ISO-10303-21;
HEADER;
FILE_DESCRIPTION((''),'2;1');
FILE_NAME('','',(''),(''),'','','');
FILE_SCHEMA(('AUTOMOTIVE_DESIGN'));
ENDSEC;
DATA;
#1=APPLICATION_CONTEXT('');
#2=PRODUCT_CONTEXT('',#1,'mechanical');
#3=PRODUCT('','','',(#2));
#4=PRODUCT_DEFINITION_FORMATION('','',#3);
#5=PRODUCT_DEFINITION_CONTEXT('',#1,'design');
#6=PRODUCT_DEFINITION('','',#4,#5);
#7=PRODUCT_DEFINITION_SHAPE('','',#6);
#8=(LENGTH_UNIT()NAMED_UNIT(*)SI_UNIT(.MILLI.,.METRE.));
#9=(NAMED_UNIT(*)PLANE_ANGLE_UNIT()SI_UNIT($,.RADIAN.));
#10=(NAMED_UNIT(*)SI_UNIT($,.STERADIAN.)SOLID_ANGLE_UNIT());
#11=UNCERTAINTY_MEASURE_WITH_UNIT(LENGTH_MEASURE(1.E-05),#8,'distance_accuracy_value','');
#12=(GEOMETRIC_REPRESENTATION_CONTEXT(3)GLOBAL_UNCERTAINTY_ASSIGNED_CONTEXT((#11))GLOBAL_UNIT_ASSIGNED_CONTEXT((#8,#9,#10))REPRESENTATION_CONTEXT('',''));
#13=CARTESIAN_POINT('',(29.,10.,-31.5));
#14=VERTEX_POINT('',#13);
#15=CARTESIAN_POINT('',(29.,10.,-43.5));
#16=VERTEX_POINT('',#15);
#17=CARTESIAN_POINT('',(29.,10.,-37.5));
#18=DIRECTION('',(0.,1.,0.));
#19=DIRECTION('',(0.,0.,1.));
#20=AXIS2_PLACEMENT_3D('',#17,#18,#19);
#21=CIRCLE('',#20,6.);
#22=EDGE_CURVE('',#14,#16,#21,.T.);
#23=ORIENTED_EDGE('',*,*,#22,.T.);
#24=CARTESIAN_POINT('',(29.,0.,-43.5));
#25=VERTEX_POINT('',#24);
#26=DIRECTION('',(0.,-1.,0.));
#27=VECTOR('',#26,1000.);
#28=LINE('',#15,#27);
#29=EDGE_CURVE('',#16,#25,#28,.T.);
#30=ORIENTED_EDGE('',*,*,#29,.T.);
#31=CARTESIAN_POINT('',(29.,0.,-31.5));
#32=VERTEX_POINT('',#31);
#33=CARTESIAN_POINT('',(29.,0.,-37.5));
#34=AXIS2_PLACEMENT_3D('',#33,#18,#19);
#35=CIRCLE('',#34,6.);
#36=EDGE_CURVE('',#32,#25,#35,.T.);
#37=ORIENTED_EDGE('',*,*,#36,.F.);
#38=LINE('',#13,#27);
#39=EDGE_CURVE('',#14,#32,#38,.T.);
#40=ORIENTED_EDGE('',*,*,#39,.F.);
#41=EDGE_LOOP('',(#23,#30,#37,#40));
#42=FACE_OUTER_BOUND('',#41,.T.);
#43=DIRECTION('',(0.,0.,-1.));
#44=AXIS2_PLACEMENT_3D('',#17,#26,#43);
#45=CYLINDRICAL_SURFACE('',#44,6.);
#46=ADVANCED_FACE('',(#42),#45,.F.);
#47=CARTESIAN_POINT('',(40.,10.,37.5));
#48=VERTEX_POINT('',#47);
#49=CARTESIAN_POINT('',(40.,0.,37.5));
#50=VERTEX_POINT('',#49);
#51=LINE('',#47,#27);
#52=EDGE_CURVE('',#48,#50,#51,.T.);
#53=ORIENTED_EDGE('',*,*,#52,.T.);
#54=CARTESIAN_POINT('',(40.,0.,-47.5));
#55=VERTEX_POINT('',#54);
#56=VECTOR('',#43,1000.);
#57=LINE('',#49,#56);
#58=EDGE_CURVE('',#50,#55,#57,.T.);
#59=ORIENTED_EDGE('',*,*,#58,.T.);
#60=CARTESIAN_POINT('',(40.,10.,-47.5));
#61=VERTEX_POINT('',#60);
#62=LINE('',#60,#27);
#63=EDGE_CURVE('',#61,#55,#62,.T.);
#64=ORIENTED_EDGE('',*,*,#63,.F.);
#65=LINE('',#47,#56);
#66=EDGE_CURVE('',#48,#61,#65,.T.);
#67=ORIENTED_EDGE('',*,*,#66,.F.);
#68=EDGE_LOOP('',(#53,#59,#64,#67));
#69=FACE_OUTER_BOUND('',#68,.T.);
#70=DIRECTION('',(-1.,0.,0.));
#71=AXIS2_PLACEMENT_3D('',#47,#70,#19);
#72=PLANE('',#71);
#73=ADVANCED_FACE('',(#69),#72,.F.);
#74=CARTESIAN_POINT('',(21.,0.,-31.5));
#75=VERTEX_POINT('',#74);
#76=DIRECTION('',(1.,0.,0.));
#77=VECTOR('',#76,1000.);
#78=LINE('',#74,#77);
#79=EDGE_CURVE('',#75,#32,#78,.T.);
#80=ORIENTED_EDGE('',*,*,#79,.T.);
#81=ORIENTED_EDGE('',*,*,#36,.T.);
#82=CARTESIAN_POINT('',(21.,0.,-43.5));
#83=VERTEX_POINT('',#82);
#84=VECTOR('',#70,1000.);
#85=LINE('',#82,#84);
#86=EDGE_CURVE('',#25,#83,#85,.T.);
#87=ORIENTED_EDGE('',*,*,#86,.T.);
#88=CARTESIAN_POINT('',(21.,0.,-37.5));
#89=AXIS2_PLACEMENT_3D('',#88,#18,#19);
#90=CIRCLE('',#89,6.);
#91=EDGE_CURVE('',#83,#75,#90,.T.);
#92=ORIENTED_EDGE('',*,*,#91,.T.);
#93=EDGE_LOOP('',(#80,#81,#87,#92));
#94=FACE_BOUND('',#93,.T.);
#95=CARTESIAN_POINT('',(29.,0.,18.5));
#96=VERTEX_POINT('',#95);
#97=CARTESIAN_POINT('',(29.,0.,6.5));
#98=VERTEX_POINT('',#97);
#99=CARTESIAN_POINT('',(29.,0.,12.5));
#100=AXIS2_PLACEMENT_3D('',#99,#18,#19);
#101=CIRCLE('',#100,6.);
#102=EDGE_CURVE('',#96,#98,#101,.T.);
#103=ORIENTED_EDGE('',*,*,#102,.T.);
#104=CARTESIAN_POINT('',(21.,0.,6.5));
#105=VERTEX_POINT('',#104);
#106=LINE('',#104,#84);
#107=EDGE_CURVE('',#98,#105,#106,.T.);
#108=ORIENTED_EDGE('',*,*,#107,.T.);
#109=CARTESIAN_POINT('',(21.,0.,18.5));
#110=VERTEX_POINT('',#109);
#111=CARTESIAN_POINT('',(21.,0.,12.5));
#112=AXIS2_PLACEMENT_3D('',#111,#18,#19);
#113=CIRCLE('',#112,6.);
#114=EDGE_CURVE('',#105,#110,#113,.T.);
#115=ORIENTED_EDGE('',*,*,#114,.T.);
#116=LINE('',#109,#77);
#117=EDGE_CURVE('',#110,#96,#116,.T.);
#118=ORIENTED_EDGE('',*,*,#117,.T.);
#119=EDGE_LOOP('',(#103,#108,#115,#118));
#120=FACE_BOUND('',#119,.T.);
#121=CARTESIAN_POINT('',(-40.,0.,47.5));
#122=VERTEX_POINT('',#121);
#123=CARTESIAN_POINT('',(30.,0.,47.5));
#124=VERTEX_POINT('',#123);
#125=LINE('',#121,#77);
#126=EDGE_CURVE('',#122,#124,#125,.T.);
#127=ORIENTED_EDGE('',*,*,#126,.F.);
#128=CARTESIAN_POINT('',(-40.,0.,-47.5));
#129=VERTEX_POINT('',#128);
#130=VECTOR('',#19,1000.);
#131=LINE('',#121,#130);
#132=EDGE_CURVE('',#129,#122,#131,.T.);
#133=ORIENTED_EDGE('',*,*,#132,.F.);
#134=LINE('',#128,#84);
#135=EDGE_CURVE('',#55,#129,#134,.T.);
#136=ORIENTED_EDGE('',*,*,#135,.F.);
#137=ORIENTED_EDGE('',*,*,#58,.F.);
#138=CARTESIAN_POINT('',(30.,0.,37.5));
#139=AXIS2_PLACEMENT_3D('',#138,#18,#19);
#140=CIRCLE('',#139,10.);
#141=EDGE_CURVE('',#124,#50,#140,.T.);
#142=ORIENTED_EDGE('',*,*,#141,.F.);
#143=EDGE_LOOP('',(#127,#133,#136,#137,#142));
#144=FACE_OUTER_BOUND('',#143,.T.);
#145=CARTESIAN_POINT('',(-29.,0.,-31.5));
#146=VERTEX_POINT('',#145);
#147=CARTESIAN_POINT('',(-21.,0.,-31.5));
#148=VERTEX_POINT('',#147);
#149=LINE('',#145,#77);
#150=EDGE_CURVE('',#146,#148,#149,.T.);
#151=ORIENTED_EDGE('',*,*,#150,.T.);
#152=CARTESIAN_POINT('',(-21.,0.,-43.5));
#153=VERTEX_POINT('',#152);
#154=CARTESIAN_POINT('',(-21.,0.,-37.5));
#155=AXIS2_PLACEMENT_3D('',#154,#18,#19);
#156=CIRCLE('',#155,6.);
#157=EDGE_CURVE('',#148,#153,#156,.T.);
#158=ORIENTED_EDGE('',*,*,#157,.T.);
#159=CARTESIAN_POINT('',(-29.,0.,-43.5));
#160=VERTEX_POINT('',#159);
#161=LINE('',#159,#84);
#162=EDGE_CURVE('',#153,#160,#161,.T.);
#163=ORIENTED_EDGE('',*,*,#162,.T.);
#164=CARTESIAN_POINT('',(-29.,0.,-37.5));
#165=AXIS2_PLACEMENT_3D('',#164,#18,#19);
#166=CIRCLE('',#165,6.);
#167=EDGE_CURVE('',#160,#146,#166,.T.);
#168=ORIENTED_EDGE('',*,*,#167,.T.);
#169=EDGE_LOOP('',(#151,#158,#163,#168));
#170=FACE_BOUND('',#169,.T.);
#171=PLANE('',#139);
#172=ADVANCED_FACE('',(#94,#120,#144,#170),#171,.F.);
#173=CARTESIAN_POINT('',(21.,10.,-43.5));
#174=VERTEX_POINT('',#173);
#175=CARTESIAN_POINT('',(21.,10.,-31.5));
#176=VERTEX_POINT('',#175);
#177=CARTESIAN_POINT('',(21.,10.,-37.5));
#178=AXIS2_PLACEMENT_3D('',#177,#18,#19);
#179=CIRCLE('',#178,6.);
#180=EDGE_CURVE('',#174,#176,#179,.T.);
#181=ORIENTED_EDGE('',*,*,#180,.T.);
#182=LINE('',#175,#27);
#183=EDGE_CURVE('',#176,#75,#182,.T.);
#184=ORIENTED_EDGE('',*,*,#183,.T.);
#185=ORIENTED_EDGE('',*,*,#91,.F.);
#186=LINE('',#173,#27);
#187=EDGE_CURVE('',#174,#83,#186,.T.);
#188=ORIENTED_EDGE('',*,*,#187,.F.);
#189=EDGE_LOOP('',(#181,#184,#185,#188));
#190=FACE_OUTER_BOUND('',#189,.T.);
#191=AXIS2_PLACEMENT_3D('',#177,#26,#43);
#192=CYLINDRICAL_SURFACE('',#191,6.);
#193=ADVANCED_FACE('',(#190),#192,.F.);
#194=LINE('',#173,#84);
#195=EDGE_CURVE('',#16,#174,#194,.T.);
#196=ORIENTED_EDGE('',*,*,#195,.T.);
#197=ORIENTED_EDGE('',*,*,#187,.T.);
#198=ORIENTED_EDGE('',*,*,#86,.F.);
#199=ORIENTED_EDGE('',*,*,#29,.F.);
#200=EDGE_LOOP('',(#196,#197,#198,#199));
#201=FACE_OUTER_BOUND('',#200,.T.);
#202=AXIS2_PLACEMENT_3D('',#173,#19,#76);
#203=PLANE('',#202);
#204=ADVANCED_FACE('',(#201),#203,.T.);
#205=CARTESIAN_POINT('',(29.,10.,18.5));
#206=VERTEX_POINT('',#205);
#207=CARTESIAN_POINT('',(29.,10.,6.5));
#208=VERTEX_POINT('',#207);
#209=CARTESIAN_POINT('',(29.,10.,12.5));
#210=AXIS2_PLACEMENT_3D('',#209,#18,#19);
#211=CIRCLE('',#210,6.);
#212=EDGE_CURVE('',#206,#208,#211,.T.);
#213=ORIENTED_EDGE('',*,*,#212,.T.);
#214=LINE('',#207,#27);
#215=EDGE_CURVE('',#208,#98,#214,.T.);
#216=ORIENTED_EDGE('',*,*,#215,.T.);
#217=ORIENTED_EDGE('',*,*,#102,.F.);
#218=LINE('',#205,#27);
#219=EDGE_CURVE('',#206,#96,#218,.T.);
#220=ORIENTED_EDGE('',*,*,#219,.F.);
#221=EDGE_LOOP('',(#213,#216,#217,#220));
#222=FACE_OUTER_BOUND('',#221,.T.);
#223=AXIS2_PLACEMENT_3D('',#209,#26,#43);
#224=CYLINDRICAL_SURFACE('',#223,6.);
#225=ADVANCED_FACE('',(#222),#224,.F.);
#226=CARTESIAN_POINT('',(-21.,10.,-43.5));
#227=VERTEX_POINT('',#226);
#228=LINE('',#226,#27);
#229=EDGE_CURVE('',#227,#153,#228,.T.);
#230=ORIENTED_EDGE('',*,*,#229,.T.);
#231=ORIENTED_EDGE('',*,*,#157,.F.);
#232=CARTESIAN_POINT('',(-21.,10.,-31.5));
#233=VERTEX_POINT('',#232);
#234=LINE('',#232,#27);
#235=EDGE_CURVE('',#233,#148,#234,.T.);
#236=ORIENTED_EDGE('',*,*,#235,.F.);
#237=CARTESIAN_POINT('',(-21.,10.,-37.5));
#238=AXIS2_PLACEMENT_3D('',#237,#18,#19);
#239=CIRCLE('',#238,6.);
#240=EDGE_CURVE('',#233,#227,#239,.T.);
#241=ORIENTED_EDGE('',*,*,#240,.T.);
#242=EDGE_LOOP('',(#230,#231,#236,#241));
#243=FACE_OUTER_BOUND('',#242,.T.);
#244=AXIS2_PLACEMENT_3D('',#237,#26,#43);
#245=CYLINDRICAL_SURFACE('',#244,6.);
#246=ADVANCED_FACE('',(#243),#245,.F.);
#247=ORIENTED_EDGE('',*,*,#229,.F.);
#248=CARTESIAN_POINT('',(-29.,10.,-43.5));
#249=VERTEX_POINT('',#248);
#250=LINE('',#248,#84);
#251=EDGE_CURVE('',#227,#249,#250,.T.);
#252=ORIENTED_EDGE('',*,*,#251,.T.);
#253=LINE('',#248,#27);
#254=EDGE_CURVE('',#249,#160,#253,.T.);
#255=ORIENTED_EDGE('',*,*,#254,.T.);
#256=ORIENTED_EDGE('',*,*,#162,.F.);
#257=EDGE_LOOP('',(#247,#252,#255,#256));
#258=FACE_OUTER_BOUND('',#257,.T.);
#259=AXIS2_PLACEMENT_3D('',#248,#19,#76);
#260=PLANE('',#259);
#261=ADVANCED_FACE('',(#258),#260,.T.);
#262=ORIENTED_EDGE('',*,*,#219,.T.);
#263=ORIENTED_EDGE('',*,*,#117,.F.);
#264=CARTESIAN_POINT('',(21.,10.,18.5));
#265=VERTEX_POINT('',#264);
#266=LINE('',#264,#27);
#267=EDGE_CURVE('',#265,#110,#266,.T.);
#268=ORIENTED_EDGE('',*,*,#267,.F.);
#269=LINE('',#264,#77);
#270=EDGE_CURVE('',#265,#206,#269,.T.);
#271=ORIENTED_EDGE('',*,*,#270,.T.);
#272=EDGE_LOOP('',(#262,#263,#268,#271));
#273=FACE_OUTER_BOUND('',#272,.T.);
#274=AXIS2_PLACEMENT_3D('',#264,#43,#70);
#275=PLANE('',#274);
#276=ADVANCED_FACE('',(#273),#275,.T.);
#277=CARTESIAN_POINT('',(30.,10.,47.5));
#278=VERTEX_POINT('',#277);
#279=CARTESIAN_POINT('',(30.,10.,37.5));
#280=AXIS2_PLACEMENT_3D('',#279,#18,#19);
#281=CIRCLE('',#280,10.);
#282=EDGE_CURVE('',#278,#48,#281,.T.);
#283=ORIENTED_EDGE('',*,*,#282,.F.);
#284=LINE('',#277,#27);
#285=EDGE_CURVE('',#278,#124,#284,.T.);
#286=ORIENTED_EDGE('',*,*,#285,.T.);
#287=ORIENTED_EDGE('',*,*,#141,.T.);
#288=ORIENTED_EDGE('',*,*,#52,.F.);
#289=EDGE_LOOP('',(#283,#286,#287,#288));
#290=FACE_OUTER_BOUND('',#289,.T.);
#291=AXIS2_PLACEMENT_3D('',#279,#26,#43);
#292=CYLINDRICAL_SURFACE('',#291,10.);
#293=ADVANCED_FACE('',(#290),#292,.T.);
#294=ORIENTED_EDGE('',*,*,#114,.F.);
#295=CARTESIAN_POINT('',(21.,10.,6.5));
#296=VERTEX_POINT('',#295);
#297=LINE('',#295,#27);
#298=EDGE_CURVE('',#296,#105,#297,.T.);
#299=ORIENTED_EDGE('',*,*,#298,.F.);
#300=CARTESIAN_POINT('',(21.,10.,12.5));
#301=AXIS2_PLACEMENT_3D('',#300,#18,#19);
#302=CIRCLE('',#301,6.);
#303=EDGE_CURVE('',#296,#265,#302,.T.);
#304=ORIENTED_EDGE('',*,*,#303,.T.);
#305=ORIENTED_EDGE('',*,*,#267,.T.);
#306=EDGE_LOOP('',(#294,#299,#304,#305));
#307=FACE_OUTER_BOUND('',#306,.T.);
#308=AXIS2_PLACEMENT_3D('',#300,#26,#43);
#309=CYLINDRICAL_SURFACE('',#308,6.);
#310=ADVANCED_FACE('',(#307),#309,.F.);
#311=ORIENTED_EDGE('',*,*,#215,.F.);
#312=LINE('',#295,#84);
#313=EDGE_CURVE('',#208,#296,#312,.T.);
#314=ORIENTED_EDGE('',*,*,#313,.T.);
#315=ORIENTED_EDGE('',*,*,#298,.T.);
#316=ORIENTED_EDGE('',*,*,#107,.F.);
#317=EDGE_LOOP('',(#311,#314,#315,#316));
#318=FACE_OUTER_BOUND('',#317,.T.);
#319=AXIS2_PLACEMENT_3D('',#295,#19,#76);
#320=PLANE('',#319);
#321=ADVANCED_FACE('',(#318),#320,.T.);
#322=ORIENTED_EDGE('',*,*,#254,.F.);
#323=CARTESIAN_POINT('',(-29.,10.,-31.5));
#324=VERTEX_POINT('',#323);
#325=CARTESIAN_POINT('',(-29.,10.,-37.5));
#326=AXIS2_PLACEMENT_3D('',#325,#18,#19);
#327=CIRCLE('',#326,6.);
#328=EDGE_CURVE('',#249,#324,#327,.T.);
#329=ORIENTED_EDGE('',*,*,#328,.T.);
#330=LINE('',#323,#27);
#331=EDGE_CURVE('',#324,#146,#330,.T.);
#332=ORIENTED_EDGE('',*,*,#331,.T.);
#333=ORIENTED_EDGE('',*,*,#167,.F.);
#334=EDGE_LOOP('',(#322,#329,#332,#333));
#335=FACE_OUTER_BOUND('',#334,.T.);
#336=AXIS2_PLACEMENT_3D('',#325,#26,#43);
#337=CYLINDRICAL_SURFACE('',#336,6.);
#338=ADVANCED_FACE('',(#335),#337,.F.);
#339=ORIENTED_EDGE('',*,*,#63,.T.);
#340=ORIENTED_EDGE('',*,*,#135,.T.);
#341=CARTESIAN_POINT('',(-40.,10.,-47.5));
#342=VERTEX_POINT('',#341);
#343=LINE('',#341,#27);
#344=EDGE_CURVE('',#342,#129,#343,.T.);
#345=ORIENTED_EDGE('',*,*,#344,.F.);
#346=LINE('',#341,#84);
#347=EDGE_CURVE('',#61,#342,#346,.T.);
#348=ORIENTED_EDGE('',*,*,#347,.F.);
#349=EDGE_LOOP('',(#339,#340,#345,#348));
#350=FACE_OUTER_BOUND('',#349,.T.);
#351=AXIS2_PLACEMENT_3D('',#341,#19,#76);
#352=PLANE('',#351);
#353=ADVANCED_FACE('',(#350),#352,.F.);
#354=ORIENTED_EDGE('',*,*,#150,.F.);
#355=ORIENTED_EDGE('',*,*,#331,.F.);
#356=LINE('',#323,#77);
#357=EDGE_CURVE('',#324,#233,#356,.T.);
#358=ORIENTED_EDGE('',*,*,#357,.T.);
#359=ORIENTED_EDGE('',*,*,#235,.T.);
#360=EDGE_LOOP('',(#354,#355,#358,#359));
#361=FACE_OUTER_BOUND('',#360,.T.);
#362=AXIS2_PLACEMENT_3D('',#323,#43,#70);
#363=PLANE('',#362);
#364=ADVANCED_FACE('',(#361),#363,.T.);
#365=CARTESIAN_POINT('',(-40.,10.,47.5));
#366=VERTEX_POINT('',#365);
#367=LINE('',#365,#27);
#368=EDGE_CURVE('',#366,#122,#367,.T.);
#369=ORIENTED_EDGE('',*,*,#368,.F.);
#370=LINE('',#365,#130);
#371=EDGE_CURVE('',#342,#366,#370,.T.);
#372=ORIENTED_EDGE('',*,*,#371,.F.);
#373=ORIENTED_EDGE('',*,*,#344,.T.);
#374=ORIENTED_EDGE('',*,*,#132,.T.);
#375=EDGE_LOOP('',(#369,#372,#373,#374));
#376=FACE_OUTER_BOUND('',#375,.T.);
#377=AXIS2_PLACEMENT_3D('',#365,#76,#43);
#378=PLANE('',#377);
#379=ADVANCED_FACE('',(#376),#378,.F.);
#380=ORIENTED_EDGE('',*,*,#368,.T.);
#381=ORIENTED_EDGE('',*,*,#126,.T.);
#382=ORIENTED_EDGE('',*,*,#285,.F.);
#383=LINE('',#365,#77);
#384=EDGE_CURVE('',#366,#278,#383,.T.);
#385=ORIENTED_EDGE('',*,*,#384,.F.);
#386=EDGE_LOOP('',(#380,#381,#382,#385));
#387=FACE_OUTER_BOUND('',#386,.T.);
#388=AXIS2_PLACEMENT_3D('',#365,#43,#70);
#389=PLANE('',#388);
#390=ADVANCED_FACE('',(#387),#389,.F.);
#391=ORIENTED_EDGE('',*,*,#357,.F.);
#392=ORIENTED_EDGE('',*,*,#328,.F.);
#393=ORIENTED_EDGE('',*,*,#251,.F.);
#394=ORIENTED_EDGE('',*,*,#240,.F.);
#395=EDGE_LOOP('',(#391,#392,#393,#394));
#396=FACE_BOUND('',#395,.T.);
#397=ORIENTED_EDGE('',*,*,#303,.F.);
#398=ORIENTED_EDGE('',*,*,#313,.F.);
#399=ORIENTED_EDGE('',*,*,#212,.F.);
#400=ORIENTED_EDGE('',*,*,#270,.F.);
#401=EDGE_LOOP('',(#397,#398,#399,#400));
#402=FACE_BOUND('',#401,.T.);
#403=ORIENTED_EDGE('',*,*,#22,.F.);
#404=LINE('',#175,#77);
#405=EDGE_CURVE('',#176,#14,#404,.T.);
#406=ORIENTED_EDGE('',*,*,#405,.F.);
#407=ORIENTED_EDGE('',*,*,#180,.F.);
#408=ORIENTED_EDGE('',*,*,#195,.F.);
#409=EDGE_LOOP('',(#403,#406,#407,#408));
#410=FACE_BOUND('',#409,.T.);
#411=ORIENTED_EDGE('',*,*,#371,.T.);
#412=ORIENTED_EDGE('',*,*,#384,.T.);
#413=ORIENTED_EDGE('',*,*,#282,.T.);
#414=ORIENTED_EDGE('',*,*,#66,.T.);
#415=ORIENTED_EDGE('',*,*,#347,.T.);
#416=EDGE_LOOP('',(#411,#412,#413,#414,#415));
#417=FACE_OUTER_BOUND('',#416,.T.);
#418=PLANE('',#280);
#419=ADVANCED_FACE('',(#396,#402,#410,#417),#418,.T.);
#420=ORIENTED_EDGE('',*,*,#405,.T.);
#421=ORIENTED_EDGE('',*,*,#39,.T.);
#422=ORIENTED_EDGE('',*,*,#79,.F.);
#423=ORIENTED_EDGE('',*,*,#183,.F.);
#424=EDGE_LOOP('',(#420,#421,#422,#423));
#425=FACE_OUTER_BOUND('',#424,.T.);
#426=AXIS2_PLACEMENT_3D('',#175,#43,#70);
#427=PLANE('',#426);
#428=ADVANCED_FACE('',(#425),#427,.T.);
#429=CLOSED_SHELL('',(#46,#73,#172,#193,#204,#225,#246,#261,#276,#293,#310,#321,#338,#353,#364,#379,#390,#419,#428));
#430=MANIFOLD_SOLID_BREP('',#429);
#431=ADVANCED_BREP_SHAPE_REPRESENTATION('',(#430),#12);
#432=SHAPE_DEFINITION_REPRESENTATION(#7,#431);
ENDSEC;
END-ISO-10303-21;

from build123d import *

# Parameters (mm, degrees)
BOSS_EXTRUDE1_DEPTH = 10


with BuildPart() as part:
    # Sketch1 → Boss-Extrude1 (new body)
    with BuildSketch(Plane(origin=(0, 0, 0), x_dir=(1, 0, 0), z_dir=(0, 1, 0))):
        with BuildLine():
            Line((-40, -47.5), (30, -47.5))
            ThreePointArc((30, -47.5), (37.071067812, -44.571067812), (40, -37.5))
            Line((40, -37.5), (40, 47.5))
            Line((40, 47.5), (-40, 47.5))
            Line((-40, 47.5), (-40, -47.5))
        make_face()
        with BuildLine():
            Line((-29, 43.5), (-21, 43.5))
            ThreePointArc((-21, 43.5), (-15, 37.5), (-21, 31.5))
            Line((-21, 31.5), (-29, 31.5))
            ThreePointArc((-29, 31.5), (-35, 37.5), (-29, 43.5))
        make_face(mode=Mode.SUBTRACT)
        with BuildLine():
            Line((21, 31.5), (29, 31.5))
            ThreePointArc((29, 31.5), (35, 37.5), (29, 43.5))
            Line((29, 43.5), (21, 43.5))
            ThreePointArc((21, 43.5), (15, 37.5), (21, 31.5))
        make_face(mode=Mode.SUBTRACT)
        with BuildLine():
            Line((21, -18.5), (29, -18.5))
            ThreePointArc((29, -18.5), (35, -12.5), (29, -6.5))
            Line((29, -6.5), (21, -6.5))
            ThreePointArc((21, -6.5), (15, -12.5), (21, -18.5))
        make_face(mode=Mode.SUBTRACT)
    extrude(amount=BOSS_EXTRUDE1_DEPTH)


solid = part.part
